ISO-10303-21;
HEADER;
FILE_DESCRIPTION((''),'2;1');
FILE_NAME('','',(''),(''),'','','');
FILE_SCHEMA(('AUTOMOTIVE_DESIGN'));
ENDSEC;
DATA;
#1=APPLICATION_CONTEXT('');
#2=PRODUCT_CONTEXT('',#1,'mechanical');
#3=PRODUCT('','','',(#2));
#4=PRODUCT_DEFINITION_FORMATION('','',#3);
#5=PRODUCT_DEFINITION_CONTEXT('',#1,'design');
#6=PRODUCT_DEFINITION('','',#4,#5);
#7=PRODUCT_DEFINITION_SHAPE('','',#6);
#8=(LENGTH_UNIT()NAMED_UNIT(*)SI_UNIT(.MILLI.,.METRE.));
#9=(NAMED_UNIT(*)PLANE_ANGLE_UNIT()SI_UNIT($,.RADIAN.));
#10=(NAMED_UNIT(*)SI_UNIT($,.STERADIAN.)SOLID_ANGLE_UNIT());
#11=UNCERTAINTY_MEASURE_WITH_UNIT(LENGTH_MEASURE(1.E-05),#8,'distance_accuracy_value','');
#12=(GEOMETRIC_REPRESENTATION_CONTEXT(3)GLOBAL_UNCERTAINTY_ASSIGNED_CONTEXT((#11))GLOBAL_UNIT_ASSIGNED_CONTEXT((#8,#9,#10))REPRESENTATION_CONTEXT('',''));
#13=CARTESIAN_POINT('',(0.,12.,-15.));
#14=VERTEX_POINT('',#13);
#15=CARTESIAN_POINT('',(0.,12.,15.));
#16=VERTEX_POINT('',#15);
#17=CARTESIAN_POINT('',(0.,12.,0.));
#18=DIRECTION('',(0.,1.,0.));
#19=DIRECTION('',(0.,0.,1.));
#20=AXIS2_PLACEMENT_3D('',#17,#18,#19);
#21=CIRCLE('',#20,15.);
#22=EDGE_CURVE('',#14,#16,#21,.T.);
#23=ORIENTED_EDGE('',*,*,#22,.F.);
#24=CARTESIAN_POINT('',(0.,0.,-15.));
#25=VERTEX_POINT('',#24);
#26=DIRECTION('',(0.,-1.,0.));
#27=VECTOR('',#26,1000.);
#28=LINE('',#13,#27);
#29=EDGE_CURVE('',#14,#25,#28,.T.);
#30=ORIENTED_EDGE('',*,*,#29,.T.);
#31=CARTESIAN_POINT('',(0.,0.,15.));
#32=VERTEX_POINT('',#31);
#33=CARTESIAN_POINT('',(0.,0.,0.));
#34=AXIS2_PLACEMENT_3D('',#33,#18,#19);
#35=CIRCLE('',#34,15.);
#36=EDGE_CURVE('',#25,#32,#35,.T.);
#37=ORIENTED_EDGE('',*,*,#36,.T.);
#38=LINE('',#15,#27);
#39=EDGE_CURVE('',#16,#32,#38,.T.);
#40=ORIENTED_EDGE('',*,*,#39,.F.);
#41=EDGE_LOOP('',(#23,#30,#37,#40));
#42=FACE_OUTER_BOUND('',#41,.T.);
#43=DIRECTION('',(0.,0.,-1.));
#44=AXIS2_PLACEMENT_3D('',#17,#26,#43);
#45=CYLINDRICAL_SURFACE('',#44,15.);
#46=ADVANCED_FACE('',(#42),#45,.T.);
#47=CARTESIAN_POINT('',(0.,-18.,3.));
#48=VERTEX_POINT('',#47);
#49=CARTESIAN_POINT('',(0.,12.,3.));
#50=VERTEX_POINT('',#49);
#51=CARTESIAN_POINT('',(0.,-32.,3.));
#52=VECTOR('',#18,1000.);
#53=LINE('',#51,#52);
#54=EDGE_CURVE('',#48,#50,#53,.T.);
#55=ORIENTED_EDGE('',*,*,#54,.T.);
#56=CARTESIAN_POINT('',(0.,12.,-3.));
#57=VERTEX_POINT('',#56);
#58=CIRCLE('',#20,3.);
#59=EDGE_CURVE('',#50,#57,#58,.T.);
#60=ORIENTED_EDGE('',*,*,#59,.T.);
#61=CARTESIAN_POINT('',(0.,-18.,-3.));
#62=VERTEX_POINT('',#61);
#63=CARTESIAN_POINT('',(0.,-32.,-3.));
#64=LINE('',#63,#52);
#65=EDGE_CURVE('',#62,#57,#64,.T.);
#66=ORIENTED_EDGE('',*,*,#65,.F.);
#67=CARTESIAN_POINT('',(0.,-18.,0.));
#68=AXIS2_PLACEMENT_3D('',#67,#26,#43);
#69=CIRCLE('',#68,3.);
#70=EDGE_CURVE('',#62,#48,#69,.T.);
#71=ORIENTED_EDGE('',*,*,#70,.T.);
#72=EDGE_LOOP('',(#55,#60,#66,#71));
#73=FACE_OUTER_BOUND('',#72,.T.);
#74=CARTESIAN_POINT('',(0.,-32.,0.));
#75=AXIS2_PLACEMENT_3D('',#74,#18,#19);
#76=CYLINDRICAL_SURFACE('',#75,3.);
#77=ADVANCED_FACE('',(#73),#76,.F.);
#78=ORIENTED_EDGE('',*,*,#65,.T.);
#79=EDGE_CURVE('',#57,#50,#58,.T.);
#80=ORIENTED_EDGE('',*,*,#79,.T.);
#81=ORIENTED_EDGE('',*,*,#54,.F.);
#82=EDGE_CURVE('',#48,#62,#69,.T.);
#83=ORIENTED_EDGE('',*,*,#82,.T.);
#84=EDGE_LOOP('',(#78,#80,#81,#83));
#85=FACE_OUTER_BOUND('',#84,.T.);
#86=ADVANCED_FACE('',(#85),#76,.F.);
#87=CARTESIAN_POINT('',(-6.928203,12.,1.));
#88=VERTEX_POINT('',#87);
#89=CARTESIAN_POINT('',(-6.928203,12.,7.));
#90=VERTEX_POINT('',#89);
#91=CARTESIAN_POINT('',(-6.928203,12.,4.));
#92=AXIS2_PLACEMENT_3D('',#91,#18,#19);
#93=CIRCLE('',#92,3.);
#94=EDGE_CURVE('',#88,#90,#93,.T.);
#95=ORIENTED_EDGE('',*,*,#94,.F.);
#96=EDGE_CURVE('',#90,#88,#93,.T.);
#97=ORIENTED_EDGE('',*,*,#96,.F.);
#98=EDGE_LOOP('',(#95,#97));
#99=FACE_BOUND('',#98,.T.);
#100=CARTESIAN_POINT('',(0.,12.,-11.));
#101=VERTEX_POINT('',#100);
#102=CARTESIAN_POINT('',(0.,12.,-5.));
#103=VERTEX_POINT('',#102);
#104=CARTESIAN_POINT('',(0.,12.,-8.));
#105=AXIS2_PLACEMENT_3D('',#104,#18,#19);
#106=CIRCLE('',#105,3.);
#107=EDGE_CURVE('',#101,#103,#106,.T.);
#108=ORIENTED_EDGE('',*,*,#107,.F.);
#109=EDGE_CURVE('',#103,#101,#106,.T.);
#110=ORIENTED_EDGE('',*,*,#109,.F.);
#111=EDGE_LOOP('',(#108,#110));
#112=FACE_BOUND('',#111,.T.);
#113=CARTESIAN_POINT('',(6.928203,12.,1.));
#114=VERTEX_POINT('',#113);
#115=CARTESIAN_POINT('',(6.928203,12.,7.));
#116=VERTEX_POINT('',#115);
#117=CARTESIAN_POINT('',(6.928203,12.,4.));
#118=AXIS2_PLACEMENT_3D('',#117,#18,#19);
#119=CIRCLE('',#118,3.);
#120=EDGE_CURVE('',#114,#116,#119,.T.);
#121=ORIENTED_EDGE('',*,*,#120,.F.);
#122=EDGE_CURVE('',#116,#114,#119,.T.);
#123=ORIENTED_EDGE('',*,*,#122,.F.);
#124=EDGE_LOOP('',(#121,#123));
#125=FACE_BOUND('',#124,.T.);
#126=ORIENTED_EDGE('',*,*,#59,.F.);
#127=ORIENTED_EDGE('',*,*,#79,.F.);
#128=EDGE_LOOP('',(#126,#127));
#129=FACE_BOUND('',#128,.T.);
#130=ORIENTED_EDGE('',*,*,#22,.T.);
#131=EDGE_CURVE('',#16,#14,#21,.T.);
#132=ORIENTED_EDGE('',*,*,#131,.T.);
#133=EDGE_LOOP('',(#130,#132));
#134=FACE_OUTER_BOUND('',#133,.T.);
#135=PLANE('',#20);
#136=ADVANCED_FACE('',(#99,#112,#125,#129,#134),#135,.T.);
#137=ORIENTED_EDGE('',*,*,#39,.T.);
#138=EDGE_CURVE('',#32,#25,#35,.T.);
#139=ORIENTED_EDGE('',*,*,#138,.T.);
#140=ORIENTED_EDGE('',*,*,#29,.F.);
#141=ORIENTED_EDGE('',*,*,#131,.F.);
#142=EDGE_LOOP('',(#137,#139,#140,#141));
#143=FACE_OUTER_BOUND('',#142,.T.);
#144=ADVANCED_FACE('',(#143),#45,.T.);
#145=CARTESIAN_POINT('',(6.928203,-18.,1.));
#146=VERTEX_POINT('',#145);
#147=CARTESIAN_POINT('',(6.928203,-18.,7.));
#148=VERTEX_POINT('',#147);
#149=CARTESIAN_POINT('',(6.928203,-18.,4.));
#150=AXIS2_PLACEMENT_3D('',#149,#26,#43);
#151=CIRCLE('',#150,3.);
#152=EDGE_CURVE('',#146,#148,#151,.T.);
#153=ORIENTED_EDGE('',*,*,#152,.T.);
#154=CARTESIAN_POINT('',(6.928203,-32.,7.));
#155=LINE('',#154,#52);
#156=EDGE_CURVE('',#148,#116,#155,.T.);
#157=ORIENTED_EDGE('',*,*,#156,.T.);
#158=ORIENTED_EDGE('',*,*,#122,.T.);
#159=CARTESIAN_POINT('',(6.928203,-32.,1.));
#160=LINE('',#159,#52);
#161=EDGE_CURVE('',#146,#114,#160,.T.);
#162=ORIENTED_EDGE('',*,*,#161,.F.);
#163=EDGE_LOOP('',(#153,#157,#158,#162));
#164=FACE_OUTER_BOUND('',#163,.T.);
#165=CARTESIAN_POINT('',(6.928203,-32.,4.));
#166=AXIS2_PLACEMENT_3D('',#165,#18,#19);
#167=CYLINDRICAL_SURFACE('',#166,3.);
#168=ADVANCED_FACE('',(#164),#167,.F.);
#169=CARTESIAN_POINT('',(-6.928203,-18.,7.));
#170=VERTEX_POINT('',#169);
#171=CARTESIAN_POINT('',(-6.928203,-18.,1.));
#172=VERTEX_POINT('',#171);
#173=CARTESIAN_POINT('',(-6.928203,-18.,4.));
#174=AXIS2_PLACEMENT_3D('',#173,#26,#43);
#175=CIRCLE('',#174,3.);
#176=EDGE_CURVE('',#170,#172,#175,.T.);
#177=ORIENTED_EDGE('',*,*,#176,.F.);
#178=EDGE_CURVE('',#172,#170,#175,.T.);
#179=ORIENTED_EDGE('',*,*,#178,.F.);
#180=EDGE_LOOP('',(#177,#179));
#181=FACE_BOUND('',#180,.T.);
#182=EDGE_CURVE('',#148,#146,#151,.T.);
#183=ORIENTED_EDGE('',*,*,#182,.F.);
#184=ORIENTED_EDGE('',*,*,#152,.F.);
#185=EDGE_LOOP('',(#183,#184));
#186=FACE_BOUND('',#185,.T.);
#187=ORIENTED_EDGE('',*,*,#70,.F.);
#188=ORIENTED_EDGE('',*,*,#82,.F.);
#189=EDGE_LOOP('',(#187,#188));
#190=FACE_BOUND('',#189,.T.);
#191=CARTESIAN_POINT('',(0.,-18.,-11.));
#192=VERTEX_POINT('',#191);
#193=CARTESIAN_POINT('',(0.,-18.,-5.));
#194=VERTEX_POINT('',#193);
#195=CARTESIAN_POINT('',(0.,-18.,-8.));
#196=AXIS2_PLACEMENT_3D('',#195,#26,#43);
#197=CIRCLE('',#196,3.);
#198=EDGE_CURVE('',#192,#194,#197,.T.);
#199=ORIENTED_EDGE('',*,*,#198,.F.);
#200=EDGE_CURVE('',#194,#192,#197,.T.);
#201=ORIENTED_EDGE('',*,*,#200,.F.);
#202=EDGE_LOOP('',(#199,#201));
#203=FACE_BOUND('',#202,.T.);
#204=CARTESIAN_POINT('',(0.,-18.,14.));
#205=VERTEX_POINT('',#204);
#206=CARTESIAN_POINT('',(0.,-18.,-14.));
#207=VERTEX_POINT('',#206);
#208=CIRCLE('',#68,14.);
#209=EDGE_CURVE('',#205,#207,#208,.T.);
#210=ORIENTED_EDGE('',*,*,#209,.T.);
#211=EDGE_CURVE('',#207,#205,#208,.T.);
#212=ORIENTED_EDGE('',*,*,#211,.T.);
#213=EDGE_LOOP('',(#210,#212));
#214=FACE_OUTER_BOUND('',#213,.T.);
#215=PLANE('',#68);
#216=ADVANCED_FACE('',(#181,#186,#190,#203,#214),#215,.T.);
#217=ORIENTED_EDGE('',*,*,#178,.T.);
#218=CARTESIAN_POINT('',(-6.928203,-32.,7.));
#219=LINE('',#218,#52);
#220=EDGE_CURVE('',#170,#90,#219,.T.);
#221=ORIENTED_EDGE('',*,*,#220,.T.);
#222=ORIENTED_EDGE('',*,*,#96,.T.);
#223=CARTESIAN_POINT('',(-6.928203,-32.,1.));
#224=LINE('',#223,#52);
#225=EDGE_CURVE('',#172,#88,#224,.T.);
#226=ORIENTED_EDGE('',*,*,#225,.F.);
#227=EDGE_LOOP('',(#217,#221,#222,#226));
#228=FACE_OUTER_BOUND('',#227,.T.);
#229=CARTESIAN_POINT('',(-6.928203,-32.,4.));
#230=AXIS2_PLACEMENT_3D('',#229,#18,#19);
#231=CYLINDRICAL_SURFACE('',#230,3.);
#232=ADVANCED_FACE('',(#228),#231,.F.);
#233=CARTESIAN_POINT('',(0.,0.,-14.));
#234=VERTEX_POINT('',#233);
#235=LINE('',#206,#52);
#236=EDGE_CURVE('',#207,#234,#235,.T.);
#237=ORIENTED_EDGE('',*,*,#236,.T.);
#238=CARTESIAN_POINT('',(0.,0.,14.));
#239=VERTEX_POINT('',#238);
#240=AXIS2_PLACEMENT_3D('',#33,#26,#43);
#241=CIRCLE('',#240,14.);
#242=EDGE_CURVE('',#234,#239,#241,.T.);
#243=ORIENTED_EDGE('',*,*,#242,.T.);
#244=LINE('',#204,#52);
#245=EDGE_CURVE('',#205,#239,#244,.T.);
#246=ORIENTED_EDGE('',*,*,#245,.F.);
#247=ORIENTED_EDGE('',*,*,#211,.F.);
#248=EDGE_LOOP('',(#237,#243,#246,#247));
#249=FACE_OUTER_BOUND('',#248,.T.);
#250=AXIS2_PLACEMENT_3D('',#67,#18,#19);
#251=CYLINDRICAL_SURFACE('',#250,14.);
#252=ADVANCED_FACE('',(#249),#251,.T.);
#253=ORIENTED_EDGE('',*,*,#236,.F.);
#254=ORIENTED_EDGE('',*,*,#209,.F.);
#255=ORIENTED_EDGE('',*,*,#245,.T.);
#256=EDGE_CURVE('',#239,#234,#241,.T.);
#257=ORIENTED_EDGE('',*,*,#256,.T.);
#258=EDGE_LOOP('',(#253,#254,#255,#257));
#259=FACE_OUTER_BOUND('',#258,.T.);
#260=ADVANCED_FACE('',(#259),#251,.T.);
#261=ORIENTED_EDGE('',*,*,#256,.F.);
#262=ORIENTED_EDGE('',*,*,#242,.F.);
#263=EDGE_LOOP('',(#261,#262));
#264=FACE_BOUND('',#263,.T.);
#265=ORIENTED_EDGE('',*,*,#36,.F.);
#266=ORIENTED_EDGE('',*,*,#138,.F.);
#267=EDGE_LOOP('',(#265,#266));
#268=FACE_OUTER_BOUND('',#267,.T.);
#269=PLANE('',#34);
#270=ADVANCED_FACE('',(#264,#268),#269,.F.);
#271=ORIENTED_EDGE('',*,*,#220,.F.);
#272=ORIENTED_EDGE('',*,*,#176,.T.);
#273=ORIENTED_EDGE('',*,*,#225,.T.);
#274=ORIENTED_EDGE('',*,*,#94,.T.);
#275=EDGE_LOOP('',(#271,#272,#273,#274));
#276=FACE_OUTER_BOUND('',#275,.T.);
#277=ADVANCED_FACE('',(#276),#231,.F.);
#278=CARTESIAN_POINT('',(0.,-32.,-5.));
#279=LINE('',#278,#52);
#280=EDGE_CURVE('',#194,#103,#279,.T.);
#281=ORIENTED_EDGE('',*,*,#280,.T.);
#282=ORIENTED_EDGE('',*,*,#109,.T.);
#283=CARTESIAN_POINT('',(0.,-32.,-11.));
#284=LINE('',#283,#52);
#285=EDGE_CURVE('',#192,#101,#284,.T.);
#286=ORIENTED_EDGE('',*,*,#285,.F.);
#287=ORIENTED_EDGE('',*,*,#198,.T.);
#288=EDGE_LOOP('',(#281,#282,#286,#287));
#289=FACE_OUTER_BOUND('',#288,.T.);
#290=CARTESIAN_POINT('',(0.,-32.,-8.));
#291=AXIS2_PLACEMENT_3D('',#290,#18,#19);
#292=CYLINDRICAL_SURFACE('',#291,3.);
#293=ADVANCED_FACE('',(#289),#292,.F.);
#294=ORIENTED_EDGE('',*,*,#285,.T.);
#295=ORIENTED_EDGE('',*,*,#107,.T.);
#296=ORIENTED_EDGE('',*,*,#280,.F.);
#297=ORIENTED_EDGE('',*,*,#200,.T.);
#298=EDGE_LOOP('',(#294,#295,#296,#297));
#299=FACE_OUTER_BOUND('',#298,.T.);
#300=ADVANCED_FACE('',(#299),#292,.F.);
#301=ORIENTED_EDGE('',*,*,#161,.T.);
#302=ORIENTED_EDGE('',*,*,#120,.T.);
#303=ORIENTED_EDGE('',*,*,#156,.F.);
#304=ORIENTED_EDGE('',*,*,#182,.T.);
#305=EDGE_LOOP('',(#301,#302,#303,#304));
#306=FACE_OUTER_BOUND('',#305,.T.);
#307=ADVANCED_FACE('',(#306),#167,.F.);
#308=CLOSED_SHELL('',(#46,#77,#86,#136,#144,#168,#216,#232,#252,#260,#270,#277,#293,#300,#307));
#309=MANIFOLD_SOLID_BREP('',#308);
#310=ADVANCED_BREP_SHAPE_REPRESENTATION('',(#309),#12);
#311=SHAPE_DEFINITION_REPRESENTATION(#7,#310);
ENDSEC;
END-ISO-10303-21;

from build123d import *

# Parameters (mm, degrees)
UPPER_BODY_PROFILE_30_R         = 15
UPPER_BODY_30X12_DEPTH          = 12
LOWER_BODY_PROFILE_28_R         = 14
LOWER_BODY_28X18_DEPTH          = 18
OFFSET_HOLES_PROFILE_3X_6_R     = 3
OFFSET_THROUGH_HOLES_3X_6_DEPTH = 44
CENTER_HOLE_PROFILE_6_R         = 3
CENTER_THROUGH_HOLE_6_DEPTH     = 44


with BuildPart() as part:
    # Upper Body Profile Ø30 → Upper Body Ø30x12 (new body)
    with BuildSketch(Plane(origin=(0, 0, 0), x_dir=(1, 0, 0), z_dir=(0, 1, 0))):
        with Locations(Location((0, 0, 0), (0, 0, 270))):
            Circle(UPPER_BODY_PROFILE_30_R)
    extrude(amount=UPPER_BODY_30X12_DEPTH)

    # Lower Body Profile Ø28 → Lower Body Ø28x18 (add)
    with BuildSketch(Plane.XZ):
        with Locations(Location((0, 0, 0), (0, 0, 270))):
            Circle(LOWER_BODY_PROFILE_28_R)
    extrude(amount=LOWER_BODY_28X18_DEPTH)

    # Offset Holes Profile 3xØ6 → Offset Through Holes 3xØ6 (cut)
    with BuildSketch(Plane(origin=(0, 12, 0), x_dir=(1, 0, 0), z_dir=(0, 1, 0))):
        with Locations(Location((0, 8, 0), (0, 0, 270))):
            Circle(OFFSET_HOLES_PROFILE_3X_6_R)
        with Locations(Location((6.92820323, -4, 0), (0, 0, 270))):
            Circle(OFFSET_HOLES_PROFILE_3X_6_R)
        with Locations(Location((-6.92820323, -4, 0), (0, 0, 270))):
            Circle(OFFSET_HOLES_PROFILE_3X_6_R)
    extrude(amount=-OFFSET_THROUGH_HOLES_3X_6_DEPTH, mode=Mode.SUBTRACT)

    # Center Hole Profile Ø6 → Center Through Hole Ø6 (cut)
    with BuildSketch(Plane(origin=(0, 12, 0), x_dir=(1, 0, 0), z_dir=(0, 1, 0))):
        with Locations(Location((0, 0, 0), (0, 0, 270))):
            Circle(CENTER_HOLE_PROFILE_6_R)
    extrude(amount=-CENTER_THROUGH_HOLE_6_DEPTH, mode=Mode.SUBTRACT)


solid = part.part
